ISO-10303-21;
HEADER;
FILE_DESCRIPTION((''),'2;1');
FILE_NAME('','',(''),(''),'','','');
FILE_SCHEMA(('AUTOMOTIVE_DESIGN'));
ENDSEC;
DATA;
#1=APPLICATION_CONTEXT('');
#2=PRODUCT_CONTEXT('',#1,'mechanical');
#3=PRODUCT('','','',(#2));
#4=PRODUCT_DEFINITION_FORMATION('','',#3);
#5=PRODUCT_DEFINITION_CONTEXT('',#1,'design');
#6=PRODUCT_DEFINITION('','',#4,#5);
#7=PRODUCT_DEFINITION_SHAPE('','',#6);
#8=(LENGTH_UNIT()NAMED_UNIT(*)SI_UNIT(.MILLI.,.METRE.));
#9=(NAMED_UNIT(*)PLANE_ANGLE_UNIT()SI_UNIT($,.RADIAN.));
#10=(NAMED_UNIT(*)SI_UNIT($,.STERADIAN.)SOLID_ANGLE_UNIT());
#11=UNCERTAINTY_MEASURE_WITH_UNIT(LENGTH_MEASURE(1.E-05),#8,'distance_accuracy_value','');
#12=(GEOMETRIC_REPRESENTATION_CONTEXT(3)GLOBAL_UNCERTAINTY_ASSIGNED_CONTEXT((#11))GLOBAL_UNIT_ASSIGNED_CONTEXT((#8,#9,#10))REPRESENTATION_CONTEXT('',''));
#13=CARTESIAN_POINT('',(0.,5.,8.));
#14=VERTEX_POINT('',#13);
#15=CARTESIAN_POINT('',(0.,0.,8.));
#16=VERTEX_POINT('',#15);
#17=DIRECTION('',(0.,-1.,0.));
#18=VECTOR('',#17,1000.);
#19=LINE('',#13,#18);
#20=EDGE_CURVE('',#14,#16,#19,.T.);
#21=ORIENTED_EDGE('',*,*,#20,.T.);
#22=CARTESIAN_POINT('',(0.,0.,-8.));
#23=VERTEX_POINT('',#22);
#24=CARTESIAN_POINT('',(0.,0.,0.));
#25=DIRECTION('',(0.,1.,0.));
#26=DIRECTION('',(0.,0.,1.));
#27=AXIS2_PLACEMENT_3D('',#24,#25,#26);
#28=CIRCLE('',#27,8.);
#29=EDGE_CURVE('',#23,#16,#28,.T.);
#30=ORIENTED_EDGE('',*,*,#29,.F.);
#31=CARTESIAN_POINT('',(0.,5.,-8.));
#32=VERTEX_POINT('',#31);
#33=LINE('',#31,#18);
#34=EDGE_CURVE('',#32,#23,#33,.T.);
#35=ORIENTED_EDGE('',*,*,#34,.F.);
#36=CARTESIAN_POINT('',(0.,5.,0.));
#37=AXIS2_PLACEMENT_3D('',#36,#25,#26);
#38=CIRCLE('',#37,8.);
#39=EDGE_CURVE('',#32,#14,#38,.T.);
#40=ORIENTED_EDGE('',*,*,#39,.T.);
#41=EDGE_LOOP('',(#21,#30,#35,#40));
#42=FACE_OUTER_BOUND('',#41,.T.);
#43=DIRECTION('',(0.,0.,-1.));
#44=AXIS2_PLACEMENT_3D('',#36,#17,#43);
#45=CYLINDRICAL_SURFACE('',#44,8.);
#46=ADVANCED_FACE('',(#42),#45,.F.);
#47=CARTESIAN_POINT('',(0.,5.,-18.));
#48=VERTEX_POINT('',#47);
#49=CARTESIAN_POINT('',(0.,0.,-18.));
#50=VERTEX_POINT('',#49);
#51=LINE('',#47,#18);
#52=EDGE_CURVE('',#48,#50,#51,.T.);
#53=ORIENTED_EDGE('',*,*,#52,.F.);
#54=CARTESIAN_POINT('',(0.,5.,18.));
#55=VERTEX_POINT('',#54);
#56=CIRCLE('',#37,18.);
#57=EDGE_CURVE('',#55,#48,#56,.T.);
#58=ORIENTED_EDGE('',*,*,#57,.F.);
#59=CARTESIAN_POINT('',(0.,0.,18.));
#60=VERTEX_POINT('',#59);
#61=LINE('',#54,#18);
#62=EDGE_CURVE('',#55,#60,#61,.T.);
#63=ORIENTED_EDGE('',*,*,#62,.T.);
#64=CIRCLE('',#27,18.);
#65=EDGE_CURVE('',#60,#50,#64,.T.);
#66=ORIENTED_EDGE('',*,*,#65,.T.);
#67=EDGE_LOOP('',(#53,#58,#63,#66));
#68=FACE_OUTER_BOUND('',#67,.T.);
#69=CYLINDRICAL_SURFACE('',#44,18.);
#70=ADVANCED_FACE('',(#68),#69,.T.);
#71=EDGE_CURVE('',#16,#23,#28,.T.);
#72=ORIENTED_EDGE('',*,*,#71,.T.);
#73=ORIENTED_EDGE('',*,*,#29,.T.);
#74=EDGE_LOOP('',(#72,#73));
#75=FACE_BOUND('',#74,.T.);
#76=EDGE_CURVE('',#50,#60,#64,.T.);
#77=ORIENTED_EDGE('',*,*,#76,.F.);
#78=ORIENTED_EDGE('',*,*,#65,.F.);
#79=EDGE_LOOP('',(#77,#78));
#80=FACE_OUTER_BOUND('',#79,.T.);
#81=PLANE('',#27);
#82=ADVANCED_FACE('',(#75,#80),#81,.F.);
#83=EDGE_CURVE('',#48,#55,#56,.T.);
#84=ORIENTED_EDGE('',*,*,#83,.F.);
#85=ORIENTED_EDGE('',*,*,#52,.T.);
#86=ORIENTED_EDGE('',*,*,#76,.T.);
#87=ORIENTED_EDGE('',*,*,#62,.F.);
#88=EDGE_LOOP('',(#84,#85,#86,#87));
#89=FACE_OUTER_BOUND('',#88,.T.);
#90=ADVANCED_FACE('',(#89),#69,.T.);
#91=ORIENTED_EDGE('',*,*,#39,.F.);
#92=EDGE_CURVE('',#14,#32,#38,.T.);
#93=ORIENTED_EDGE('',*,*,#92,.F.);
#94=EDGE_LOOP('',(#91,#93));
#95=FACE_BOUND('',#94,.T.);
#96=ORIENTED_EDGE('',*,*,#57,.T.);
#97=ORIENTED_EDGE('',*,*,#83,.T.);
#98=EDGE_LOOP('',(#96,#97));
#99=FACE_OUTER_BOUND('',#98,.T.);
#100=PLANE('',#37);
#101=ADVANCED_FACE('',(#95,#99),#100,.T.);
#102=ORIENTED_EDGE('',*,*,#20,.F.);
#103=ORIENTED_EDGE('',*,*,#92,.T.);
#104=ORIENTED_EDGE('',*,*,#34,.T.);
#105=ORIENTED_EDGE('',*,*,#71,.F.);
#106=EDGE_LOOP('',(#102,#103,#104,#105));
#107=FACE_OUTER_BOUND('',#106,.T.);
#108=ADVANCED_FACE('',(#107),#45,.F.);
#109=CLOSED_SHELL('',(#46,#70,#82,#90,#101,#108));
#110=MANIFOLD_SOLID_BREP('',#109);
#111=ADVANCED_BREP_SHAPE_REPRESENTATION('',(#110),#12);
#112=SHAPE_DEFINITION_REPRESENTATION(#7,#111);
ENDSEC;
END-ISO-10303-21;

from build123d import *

# Parameters (mm, degrees)
SKETCH1_R           = 18
SKETCH1_R_2         = 8
BOSS_EXTRUDE1_DEPTH = 5


with BuildPart() as part:
    # Sketch1 → Boss-Extrude1 (new body)
    with BuildSketch(Plane(origin=(0, 0, 0), x_dir=(1, 0, 0), z_dir=(0, 1, 0))):
        with Locations(Location((0, 0, 0), (0, 0, 270))):
            Circle(SKETCH1_R)
        with Locations(Location((0, 0, 0), (0, 0, 270))):
            Circle(SKETCH1_R_2, mode=Mode.SUBTRACT)
    extrude(amount=BOSS_EXTRUDE1_DEPTH)


solid = part.part
